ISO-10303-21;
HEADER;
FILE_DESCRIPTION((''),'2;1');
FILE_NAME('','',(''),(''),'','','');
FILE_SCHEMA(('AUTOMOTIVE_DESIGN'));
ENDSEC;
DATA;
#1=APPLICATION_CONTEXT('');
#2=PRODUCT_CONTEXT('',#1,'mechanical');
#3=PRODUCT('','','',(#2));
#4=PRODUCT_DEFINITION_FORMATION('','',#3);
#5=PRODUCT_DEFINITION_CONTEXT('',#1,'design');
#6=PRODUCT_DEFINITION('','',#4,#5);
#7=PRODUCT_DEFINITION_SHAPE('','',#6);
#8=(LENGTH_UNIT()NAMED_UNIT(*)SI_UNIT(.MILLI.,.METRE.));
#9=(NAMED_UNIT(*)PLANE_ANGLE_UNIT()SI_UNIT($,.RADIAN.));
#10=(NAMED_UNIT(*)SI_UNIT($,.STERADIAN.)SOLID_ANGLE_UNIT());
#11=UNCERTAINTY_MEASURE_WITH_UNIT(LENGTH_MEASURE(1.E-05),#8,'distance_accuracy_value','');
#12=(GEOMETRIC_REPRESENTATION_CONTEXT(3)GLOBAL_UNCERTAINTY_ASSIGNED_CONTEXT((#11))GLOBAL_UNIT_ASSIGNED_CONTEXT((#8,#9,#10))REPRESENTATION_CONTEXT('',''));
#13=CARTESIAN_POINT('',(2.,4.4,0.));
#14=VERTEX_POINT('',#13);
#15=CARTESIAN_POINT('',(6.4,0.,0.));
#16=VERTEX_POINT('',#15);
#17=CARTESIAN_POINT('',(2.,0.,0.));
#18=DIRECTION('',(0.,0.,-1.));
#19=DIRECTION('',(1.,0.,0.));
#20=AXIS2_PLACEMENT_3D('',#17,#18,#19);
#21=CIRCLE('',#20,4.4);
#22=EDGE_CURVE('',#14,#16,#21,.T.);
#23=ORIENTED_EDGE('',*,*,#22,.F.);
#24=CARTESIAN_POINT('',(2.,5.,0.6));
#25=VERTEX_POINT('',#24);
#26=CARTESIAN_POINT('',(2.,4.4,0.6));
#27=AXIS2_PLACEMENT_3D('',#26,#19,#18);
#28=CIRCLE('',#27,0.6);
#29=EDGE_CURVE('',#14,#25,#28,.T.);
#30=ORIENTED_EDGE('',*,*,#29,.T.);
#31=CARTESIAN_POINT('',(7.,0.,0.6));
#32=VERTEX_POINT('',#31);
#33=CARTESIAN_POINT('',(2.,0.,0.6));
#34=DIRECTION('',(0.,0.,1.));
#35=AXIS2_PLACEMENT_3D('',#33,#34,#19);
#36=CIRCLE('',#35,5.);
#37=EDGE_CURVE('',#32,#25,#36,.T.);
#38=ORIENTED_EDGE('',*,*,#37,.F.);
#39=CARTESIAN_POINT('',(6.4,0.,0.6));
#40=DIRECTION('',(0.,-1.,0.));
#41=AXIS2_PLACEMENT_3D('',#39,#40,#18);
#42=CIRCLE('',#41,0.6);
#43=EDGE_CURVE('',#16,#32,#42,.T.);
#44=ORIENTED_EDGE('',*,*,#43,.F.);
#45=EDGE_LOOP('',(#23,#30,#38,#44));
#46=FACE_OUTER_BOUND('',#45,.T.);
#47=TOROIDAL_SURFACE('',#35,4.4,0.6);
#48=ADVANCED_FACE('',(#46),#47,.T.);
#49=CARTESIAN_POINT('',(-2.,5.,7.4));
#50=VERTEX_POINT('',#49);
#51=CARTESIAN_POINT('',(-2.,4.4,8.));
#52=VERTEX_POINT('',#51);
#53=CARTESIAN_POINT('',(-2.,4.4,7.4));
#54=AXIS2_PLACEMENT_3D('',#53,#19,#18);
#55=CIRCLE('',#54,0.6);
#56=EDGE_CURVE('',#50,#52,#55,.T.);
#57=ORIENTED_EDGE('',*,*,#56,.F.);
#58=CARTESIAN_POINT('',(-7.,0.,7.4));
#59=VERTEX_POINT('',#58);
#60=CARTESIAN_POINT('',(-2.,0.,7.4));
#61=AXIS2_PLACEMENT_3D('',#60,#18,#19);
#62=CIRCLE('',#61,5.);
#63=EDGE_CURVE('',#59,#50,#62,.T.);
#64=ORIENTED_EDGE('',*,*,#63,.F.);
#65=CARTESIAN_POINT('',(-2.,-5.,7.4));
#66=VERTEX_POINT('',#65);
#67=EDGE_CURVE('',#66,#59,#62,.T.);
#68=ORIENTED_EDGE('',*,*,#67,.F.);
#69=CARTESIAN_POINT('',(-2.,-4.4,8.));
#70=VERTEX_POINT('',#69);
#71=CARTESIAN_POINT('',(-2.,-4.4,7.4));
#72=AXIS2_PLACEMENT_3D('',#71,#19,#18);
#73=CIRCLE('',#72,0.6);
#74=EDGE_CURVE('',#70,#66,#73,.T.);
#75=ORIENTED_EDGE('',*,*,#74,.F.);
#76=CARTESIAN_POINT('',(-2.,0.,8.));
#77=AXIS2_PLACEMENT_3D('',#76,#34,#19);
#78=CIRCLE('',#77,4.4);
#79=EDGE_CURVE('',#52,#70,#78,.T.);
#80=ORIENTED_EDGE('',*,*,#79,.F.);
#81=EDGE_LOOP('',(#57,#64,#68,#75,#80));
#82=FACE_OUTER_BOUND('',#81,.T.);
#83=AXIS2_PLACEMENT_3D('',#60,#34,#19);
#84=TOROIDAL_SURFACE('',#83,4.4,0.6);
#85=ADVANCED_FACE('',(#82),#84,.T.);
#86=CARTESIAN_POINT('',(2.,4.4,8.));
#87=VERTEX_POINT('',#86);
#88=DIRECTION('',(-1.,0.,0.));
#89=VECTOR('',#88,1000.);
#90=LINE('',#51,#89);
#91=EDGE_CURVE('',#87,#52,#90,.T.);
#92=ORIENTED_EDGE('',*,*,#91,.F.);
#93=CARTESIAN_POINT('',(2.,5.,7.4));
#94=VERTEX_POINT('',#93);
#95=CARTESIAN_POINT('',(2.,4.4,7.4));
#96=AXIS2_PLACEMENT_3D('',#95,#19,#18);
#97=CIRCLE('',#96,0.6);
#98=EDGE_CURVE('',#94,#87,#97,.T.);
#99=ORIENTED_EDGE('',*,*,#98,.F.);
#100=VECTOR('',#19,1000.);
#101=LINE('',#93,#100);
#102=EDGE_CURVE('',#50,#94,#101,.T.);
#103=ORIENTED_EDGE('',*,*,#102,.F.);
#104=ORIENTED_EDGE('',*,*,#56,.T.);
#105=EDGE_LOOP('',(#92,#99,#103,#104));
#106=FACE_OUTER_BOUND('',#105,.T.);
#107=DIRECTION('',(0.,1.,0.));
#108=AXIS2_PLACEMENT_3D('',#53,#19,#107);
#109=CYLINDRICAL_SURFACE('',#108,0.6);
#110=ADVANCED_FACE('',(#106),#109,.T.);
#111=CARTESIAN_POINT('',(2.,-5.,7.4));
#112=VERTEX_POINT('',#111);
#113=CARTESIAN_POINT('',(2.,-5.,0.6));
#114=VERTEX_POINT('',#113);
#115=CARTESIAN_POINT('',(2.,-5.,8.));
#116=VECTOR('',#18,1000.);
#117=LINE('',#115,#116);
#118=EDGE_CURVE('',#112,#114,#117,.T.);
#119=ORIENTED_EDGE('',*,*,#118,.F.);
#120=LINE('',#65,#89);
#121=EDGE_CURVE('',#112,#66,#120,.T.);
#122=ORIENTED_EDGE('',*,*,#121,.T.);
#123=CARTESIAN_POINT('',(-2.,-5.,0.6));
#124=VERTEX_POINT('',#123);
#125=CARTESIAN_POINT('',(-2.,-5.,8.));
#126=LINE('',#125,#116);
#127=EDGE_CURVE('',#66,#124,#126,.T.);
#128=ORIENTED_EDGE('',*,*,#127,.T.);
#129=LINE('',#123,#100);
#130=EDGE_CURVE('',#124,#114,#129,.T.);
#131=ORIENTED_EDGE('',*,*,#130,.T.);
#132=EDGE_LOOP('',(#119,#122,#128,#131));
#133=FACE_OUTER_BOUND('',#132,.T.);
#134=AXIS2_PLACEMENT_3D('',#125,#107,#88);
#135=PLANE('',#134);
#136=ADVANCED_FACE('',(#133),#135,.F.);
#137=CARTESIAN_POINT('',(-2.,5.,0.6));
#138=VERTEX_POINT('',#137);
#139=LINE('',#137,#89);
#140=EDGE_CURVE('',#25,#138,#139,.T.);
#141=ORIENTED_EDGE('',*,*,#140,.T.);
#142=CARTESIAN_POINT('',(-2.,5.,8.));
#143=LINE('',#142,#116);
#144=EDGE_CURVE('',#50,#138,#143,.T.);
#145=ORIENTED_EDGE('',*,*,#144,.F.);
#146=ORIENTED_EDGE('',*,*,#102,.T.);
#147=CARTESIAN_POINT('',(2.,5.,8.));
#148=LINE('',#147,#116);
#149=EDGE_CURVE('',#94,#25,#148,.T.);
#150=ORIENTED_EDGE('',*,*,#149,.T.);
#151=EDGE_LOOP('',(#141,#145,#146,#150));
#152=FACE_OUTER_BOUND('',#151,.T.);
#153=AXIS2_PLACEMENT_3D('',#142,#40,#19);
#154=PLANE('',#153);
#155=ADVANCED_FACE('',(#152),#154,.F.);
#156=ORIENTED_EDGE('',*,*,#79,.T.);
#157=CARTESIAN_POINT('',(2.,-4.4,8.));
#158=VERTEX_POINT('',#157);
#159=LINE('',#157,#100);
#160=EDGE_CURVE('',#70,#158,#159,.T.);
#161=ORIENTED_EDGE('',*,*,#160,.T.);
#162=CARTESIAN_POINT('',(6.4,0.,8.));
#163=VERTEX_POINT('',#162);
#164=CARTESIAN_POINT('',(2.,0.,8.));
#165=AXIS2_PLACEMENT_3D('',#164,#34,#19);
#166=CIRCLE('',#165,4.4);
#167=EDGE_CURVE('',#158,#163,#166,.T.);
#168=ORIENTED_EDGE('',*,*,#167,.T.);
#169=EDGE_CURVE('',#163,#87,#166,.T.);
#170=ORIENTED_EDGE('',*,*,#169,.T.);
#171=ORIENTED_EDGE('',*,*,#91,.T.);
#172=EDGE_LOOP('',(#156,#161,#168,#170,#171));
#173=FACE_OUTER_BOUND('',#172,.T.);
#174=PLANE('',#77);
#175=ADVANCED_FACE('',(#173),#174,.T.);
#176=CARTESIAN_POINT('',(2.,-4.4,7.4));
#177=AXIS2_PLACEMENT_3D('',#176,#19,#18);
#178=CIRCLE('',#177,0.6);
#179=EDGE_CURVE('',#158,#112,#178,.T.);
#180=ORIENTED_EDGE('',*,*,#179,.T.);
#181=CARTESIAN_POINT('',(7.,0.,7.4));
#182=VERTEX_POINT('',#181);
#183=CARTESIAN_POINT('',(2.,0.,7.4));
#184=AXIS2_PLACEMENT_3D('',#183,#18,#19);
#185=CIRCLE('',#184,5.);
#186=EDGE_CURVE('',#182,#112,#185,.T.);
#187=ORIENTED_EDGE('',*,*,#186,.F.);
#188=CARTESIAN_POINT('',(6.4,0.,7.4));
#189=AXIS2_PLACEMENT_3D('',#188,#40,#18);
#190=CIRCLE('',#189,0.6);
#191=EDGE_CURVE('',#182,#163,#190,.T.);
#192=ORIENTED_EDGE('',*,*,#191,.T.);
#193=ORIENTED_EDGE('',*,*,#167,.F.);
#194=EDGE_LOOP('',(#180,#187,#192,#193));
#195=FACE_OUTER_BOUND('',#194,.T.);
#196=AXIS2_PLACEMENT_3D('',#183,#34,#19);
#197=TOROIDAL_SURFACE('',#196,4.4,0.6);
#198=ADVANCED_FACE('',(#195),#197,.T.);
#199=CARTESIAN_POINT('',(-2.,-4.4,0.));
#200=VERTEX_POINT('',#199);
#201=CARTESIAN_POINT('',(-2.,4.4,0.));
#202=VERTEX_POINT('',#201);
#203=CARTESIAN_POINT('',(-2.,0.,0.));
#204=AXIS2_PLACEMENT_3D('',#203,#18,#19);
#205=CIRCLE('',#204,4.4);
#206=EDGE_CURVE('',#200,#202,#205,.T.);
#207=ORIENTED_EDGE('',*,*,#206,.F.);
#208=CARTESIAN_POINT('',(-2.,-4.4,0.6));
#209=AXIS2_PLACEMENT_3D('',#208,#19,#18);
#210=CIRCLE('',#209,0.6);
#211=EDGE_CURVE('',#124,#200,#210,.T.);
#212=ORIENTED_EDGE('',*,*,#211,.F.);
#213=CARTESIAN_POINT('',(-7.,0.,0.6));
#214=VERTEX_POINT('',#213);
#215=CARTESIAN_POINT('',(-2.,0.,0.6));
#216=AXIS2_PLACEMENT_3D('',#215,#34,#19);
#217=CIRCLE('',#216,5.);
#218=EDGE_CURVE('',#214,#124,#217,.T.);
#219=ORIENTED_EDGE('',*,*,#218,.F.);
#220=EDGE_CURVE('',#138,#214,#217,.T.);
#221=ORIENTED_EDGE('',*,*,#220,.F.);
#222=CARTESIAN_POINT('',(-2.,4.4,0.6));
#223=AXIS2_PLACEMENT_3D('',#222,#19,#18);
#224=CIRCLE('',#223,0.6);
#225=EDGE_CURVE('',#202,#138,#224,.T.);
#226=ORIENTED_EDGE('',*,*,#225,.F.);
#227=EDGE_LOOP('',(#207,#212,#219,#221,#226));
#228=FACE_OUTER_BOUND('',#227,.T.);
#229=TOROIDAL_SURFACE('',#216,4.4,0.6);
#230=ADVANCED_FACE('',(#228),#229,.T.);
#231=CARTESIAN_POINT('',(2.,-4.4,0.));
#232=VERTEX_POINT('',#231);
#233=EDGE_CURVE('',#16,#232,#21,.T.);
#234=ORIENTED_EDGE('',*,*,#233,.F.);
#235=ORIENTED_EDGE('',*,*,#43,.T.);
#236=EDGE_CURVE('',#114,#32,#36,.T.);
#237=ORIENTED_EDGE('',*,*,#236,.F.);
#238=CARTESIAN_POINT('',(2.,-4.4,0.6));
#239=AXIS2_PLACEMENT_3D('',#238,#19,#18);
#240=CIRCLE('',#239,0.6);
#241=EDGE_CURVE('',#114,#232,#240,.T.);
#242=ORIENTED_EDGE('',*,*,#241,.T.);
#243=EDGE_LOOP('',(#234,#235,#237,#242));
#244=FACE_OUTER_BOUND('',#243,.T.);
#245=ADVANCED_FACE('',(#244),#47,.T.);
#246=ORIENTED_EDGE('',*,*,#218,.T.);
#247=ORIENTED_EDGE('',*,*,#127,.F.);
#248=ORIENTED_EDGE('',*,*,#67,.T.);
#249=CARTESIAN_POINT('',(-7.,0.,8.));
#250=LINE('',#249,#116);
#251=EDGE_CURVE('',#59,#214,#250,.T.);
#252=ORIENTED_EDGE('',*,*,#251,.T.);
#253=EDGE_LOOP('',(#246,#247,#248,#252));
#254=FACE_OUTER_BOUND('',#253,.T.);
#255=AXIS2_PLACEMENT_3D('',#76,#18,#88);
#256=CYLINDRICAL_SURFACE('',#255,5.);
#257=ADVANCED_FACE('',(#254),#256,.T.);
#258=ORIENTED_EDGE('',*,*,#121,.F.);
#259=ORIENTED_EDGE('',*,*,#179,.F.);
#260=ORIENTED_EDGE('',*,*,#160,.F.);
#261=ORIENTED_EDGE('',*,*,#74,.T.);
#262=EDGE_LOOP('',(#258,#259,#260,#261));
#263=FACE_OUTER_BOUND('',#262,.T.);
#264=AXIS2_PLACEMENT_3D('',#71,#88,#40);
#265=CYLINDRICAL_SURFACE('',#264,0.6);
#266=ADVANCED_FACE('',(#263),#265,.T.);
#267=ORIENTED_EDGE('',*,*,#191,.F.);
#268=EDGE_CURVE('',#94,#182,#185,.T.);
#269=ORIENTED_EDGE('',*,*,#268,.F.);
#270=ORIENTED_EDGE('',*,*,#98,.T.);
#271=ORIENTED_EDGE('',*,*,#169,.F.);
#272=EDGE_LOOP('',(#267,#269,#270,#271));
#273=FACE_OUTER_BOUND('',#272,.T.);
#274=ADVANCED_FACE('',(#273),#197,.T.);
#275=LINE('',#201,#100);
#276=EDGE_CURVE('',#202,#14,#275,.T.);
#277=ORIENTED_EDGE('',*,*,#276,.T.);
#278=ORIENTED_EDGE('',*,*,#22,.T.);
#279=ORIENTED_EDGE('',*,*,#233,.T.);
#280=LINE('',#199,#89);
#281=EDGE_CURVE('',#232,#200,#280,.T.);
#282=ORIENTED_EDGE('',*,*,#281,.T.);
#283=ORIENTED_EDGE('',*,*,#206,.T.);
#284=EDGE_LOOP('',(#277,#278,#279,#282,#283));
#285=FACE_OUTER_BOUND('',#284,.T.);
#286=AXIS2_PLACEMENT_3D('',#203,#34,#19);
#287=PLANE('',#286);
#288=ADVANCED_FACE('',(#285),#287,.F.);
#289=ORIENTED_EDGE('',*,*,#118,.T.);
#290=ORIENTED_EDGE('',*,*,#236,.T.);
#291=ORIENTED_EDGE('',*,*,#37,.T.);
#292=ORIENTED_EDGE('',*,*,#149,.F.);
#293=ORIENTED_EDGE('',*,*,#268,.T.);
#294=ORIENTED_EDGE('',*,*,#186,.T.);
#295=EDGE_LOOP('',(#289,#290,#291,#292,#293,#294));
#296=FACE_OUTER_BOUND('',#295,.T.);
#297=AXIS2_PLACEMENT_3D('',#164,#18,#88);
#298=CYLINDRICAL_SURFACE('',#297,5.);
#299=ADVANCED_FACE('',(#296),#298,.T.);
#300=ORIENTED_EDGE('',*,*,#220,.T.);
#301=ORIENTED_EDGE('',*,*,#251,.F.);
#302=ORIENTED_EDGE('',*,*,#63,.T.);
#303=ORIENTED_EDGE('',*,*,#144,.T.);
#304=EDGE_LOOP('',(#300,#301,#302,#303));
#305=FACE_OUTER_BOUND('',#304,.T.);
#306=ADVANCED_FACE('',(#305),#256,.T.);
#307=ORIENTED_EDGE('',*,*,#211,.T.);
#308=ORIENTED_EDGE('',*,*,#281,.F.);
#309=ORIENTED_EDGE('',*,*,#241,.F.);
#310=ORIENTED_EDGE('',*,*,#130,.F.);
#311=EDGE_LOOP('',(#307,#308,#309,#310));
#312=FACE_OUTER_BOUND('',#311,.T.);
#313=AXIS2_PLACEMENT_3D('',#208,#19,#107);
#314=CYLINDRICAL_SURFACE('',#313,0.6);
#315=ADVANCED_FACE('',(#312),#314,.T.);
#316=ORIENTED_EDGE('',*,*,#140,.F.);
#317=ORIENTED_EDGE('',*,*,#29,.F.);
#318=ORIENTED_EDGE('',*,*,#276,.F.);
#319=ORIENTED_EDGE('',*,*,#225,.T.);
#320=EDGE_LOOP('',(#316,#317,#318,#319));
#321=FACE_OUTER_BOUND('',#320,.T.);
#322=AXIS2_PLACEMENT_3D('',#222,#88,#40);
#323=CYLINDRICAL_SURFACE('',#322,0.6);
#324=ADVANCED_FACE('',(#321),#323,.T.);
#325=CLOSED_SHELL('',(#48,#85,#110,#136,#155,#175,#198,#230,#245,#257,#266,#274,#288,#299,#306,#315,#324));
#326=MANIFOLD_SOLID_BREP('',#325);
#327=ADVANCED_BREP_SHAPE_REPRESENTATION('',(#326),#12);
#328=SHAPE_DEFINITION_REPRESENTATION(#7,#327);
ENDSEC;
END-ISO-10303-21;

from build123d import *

# Parameters (mm, degrees)
EXTRUDE_523_DEPTH = 8
FILLET_1_R        = 0.6


with BuildPart() as part:
    # 草图1 → Extrude 523 (new body)
    with BuildSketch(Plane.XY):
        with BuildLine():
            Line((-2, 5), (2, 5))
            ThreePointArc((2, 5), (7, 0), (2, -5))
            Line((2, -5), (-2, -5))
            ThreePointArc((-2, -5), (-7, 0), (-2, 5))
        make_face()
    extrude(amount=EXTRUDE_523_DEPTH)

    # 圆角1
    fillet_1_edges = [part.edges().sort_by_distance(p)[0] for p in [
        (7, 0, 8),
        (0, 5, 8),
        (-7, 0, 8),
        (0, 5, 0),
        (7, 0, 0),
        (0, -5, 0),
        (-7, 0, 0),
        (0, -5, 8),
    ]]
    fillet(fillet_1_edges, radius=FILLET_1_R)


solid = part.part
